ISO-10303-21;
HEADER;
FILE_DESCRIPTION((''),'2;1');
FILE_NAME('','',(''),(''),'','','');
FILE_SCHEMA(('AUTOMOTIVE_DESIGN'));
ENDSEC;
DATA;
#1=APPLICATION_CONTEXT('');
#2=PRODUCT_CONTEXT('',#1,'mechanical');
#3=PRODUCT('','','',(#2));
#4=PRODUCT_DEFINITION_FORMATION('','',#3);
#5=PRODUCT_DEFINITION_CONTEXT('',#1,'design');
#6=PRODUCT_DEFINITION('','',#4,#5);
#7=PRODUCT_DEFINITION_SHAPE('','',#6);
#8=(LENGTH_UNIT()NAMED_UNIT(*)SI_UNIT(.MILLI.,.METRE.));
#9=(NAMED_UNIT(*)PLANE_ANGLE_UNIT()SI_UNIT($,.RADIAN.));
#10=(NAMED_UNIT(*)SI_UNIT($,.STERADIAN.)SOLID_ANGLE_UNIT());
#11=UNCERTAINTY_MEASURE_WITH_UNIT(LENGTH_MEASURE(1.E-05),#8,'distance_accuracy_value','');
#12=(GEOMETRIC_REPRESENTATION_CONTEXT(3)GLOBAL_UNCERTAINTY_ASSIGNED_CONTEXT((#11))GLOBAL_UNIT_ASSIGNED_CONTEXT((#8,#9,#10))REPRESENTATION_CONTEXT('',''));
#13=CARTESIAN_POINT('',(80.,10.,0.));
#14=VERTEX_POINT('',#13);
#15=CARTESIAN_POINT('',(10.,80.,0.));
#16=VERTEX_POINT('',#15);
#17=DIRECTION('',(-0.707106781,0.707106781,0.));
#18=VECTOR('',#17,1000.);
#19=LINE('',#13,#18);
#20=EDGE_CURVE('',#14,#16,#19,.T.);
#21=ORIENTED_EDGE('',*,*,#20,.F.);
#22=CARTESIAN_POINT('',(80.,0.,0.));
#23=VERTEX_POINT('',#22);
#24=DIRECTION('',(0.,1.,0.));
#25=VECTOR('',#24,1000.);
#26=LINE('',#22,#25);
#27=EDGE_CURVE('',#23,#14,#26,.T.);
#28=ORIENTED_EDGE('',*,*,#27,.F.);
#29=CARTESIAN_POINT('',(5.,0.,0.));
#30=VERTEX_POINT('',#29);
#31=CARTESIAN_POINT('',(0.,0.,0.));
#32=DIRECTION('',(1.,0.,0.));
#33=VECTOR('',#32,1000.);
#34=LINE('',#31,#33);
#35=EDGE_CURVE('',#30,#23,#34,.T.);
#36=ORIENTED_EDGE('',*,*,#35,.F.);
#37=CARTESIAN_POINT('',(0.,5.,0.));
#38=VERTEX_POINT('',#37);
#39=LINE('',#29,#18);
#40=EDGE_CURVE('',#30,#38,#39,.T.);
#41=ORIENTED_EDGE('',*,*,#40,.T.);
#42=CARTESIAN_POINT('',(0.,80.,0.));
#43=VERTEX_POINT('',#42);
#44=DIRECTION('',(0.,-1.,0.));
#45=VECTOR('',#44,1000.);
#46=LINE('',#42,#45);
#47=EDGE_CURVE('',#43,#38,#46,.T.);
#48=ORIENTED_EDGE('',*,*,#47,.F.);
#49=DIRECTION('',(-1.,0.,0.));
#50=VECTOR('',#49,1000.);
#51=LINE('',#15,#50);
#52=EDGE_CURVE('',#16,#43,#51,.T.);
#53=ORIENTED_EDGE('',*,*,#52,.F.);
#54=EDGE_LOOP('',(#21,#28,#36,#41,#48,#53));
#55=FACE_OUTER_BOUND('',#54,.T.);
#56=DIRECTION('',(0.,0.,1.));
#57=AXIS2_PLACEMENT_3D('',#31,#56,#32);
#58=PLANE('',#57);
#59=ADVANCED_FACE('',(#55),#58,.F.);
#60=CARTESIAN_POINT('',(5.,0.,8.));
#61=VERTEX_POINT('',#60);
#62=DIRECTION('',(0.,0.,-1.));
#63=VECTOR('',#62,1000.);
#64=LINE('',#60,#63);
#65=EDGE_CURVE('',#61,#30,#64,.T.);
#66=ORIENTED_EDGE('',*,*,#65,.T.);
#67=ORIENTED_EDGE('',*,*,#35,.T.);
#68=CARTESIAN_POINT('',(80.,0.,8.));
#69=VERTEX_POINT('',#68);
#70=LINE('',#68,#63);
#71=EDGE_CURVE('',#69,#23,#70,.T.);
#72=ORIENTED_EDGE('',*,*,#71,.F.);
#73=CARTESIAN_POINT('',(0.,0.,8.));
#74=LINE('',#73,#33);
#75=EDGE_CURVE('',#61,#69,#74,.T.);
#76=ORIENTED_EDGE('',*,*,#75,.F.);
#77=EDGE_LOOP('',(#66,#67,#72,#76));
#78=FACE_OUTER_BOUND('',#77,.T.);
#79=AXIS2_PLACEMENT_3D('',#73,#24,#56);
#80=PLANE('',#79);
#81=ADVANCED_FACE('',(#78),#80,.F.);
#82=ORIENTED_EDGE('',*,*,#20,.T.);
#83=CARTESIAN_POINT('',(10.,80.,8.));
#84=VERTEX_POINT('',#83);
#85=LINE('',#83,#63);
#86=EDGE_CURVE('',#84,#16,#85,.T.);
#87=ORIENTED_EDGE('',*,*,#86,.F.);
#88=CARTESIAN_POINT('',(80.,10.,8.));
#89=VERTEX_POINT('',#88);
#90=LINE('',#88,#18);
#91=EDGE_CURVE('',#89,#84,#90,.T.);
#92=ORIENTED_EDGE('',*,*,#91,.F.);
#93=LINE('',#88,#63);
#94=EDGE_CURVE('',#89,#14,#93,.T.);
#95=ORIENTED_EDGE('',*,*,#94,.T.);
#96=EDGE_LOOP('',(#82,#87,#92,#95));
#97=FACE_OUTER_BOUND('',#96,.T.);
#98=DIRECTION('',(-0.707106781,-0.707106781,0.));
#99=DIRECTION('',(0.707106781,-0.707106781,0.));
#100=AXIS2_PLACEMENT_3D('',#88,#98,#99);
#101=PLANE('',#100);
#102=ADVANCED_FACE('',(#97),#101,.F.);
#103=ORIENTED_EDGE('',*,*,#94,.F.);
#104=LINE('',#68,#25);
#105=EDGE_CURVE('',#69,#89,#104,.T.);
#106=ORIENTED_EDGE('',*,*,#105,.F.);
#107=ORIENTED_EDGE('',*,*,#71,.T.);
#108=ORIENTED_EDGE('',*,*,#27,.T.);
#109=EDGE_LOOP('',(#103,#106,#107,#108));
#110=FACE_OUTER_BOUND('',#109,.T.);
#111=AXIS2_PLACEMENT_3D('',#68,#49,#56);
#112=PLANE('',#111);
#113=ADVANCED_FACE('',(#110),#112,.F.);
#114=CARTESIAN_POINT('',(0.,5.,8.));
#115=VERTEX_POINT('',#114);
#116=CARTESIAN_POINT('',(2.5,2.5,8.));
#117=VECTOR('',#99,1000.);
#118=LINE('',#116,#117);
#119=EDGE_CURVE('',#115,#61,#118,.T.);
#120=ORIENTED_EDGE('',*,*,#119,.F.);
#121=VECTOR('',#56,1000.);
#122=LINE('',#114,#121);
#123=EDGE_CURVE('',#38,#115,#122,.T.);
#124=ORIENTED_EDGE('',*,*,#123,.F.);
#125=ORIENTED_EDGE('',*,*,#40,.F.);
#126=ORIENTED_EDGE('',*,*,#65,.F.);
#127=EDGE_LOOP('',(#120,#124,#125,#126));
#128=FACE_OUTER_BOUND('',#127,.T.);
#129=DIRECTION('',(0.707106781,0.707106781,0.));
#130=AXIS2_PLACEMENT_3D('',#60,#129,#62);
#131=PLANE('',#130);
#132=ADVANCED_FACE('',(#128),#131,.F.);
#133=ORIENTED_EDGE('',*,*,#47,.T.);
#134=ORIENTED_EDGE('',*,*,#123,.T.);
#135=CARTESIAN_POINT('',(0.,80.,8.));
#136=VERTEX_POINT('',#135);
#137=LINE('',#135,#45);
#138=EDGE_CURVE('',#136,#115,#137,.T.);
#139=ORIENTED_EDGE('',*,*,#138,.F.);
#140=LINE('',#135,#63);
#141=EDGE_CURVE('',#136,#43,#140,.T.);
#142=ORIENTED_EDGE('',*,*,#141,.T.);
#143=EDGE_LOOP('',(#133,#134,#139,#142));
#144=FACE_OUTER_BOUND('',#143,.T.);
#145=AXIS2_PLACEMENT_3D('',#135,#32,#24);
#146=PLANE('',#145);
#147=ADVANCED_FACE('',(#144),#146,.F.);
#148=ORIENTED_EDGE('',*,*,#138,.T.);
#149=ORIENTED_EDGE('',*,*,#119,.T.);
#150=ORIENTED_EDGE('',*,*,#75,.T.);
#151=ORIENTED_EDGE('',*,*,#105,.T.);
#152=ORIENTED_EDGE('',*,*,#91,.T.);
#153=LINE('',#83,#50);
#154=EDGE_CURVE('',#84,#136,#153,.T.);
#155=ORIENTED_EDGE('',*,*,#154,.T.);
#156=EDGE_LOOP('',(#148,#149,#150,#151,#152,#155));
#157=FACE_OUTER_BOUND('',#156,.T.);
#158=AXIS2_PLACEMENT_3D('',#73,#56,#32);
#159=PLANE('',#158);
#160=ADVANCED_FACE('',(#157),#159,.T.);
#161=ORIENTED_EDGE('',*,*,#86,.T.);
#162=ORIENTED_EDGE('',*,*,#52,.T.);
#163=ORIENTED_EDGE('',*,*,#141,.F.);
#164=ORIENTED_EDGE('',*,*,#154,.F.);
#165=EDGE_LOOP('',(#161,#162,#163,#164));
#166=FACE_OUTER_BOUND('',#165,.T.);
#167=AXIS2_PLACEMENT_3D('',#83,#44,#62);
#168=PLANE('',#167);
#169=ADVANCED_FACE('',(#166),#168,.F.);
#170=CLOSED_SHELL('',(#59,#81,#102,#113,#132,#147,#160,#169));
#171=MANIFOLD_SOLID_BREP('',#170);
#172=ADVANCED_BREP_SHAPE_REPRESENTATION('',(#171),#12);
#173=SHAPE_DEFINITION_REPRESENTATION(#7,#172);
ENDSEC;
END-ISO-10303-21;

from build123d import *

# Parameters (mm, degrees)
BOSS_EXTRUDE1_DEPTH = 8
CHAMFER1_SIZE       = 5


with BuildPart() as part:
    # Sketch1 → Boss-Extrude1 (new body)
    with BuildSketch(Plane.XY):
        Polygon((0, 80), (0, 0), (80, 0), (80, 10), (10, 80), align=None)
    extrude(amount=BOSS_EXTRUDE1_DEPTH)

    # Chamfer1
    chamfer1_edges = [part.edges().sort_by_distance(p)[0] for p in [
        (0, 0, 4),
    ]]
    chamfer(chamfer1_edges, length=CHAMFER1_SIZE)


solid = part.part
